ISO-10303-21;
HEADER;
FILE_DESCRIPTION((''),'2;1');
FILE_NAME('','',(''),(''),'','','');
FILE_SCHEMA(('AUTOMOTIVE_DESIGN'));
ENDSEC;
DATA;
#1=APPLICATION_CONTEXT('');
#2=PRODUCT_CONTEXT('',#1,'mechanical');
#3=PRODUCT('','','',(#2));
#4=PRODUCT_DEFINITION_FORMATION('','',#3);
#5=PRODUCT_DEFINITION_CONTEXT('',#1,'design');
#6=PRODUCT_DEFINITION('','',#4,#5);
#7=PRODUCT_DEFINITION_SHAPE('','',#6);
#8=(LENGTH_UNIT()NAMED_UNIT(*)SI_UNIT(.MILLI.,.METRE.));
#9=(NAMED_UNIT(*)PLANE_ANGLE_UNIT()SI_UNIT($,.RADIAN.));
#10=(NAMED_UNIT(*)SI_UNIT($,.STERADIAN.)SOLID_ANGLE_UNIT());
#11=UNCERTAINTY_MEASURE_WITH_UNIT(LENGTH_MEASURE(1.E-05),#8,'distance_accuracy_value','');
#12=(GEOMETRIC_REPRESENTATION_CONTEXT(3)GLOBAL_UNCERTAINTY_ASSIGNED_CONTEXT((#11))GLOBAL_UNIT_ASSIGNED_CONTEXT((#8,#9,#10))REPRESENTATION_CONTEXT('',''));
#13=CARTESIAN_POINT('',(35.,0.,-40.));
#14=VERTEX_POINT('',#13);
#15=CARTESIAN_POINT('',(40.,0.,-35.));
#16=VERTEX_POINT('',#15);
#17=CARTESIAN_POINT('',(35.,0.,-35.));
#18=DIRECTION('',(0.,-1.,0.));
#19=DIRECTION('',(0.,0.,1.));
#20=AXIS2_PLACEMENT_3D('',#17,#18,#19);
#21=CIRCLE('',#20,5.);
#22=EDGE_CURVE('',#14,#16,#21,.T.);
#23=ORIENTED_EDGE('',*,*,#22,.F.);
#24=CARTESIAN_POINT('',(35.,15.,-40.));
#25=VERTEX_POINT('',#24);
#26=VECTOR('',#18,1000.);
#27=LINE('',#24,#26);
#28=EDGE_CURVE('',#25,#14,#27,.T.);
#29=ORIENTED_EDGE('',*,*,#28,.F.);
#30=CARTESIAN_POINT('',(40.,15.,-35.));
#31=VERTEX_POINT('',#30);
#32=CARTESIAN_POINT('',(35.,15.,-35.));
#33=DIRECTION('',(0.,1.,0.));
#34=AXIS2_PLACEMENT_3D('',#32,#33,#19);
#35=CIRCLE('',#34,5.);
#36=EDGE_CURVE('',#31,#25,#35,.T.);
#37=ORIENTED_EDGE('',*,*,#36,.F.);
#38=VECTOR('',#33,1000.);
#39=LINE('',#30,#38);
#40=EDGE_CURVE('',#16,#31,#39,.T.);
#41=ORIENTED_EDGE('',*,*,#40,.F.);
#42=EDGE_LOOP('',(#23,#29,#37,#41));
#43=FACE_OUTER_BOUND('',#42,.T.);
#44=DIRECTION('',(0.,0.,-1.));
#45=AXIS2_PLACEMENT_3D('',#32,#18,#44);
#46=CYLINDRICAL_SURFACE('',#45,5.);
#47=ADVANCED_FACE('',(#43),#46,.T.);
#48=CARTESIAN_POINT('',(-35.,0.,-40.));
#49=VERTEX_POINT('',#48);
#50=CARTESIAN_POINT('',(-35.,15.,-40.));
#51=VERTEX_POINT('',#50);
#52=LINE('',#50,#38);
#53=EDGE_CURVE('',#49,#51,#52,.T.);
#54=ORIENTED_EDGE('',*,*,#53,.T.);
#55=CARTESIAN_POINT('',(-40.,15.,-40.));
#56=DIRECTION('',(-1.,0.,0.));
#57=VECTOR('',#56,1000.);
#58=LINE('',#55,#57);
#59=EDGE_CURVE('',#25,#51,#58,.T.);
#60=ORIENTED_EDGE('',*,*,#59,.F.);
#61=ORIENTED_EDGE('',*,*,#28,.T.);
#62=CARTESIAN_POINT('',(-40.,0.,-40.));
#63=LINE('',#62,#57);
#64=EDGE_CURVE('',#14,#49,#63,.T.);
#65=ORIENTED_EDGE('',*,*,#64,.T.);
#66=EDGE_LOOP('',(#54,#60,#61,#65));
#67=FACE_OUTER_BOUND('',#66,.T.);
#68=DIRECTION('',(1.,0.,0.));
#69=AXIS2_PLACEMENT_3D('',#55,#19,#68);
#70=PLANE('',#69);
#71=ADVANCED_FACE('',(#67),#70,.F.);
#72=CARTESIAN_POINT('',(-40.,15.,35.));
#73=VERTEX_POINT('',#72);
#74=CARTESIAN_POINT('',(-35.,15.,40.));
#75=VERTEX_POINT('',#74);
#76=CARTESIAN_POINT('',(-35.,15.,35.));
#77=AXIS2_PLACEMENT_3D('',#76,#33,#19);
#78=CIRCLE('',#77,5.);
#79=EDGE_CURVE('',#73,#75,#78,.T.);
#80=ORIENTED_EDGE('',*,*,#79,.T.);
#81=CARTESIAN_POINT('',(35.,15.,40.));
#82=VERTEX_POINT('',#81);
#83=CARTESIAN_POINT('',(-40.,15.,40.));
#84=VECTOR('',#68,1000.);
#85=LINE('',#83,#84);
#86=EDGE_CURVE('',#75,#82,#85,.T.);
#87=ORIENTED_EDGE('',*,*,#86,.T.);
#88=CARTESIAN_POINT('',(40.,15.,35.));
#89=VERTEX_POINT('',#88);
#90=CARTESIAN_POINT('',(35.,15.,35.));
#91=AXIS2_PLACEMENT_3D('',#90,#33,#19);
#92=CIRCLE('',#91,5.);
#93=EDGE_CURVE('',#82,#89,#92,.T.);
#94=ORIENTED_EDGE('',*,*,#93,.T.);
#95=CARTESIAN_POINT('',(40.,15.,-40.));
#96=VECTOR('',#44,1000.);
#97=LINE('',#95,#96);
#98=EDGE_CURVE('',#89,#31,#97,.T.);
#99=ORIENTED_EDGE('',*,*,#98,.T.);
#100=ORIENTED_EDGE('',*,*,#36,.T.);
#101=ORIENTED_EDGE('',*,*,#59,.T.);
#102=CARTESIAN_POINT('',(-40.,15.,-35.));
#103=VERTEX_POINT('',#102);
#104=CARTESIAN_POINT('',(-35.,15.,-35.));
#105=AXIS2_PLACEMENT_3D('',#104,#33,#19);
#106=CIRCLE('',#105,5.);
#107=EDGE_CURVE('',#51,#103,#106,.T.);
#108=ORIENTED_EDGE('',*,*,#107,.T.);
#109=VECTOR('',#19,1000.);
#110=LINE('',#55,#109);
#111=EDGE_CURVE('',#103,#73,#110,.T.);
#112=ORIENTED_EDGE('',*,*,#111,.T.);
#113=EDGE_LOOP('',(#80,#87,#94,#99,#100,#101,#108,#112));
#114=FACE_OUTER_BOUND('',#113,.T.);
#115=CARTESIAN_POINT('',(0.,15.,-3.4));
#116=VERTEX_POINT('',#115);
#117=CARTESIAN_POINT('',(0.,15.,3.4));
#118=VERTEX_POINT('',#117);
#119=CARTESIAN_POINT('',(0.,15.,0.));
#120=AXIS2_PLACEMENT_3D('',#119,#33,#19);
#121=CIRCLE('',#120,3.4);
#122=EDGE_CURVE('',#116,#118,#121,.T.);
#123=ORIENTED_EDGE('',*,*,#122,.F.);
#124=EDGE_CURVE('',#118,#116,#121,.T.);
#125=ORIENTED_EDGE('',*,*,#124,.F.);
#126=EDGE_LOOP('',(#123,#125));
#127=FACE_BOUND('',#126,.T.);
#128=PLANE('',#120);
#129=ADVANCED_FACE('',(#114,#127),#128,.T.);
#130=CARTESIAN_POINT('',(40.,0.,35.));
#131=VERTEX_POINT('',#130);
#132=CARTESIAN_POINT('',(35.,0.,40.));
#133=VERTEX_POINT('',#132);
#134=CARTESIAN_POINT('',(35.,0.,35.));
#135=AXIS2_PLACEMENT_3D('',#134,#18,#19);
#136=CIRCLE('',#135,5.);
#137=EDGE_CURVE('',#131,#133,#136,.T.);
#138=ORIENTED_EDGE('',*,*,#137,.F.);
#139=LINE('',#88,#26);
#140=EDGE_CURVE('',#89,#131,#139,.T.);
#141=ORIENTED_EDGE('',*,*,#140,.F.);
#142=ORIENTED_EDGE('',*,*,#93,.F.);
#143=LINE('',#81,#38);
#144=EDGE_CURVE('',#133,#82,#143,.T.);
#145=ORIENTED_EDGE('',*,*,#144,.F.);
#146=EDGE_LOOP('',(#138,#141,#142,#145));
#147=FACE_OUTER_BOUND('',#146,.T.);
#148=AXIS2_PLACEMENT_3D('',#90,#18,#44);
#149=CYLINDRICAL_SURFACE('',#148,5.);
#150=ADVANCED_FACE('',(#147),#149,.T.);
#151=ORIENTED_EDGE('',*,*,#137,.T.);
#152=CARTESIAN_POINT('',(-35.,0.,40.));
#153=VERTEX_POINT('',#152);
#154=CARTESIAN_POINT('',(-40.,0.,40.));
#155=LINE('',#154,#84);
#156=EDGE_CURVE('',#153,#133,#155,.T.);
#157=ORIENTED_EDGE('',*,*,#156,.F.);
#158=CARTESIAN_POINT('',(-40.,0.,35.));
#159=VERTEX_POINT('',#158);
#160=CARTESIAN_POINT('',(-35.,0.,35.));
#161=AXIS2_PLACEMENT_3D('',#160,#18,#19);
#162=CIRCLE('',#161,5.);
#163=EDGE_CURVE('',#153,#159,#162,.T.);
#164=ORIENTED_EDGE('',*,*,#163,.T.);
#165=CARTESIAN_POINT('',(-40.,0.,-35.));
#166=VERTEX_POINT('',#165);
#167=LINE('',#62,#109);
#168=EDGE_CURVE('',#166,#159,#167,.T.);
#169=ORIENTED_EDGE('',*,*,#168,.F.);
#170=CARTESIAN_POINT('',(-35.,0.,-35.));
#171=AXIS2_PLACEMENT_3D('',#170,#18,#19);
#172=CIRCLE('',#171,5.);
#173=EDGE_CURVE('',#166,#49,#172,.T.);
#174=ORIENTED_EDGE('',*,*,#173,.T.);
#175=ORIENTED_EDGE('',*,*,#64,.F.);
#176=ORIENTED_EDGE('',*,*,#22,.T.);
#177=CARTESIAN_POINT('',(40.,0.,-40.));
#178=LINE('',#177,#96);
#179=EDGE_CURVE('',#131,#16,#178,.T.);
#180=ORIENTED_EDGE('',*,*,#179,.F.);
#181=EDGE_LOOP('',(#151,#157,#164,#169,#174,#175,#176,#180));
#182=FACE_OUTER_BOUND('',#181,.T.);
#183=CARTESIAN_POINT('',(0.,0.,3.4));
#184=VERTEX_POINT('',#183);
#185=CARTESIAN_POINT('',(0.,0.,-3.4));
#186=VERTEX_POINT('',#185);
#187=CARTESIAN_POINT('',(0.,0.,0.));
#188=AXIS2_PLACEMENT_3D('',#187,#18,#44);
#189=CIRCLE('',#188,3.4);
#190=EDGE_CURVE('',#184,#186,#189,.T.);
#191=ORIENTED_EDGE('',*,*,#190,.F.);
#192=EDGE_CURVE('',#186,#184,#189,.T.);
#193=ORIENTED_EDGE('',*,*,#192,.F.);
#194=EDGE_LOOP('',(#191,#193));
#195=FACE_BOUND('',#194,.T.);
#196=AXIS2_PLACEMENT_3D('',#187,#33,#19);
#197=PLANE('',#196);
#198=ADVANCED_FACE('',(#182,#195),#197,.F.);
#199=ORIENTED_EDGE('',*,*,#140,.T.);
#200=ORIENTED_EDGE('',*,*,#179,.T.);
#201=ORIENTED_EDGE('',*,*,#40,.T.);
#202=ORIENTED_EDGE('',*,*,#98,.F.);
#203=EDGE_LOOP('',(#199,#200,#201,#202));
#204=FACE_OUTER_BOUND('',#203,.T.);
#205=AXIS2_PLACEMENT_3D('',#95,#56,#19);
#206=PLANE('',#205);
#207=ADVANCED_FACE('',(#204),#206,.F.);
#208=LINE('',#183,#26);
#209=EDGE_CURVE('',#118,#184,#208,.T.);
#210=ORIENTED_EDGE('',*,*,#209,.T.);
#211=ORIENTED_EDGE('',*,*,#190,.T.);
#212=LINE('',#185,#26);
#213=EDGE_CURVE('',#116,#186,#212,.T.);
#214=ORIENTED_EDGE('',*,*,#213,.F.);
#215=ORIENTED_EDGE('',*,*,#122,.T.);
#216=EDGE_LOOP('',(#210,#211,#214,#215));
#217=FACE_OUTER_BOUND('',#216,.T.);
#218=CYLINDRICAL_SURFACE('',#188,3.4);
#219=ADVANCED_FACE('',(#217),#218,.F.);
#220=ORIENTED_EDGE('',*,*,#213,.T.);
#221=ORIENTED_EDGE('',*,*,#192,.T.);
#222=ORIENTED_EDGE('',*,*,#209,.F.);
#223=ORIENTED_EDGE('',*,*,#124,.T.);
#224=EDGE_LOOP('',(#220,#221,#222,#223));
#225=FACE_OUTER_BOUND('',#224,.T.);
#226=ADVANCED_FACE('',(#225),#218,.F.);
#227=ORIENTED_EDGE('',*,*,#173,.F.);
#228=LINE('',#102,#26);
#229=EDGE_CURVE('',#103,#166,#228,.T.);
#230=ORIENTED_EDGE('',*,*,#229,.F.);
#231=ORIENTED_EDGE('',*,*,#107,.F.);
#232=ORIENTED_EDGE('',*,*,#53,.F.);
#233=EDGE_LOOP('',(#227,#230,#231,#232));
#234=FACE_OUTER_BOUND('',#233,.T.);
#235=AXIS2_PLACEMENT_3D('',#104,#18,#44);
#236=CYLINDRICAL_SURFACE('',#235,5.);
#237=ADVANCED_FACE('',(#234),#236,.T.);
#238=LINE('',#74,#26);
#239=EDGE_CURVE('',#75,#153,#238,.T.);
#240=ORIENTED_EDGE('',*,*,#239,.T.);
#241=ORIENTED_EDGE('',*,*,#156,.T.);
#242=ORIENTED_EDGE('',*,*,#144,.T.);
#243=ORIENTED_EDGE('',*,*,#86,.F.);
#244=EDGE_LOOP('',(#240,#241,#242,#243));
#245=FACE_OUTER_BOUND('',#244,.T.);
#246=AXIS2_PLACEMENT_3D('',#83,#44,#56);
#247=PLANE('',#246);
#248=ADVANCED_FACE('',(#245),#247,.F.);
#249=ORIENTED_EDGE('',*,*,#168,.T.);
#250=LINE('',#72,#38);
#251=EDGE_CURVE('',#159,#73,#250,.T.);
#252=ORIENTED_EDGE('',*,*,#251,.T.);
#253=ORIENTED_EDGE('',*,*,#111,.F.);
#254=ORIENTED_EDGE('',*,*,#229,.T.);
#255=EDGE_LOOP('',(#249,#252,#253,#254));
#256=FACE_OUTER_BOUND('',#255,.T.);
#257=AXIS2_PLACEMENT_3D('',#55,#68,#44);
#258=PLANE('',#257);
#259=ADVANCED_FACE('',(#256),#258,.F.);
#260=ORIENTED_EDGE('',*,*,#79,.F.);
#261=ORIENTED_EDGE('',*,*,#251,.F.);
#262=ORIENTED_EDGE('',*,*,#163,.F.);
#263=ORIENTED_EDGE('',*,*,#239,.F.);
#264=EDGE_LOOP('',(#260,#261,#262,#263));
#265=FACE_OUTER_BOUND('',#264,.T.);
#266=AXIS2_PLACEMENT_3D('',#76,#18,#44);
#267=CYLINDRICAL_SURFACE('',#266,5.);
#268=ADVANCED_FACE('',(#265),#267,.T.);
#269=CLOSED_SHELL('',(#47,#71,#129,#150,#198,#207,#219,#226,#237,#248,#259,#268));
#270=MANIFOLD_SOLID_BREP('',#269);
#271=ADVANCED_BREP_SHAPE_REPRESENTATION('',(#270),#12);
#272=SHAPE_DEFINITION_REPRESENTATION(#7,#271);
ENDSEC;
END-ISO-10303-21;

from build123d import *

# Parameters (mm, degrees)
SKETCH_1_W             = 80
SKETCH_1_H             = 80
EXTRUDE_1_DEPTH        = 15
FILLET_1_R             = 5
HOLE_WIZARD_M8_1_D     = 6.8
HOLE_WIZARD_M8_1_DEPTH = 19.75
HOLE_WIZARD_M8_1_TIP   = 2.042926105


with BuildPart() as part:
    # 草图1 → 凸台-拉伸1 (new body)
    with BuildSketch(Plane(origin=(0, 0, 0), x_dir=(1, 0, 0), z_dir=(0, 1, 0))):
        Rectangle(SKETCH_1_W, SKETCH_1_H)
    extrude(amount=EXTRUDE_1_DEPTH)

    # 圆角1
    fillet_1_edges = [part.edges().sort_by_distance(p)[0] for p in [
        (40, 7.5, 40),
        (-40, 7.5, 40),
        (-40, 7.5, -40),
        (40, 7.5, -40),
    ]]
    fillet(fillet_1_edges, radius=FILLET_1_R)

    # M8 螺纹孔1
    with Locations(Plane(origin=(0, 0, 0), x_dir=(-1, 0, 0), z_dir=(0, -1, 0))):
        with Locations((0, 0)):
            Hole(HOLE_WIZARD_M8_1_D / 2, depth=HOLE_WIZARD_M8_1_DEPTH)
            with Locations((0, 0, -(HOLE_WIZARD_M8_1_DEPTH + HOLE_WIZARD_M8_1_TIP / 2))):  # 118° drill point
                Cone(0, HOLE_WIZARD_M8_1_D / 2, HOLE_WIZARD_M8_1_TIP, mode=Mode.SUBTRACT)


solid = part.part
